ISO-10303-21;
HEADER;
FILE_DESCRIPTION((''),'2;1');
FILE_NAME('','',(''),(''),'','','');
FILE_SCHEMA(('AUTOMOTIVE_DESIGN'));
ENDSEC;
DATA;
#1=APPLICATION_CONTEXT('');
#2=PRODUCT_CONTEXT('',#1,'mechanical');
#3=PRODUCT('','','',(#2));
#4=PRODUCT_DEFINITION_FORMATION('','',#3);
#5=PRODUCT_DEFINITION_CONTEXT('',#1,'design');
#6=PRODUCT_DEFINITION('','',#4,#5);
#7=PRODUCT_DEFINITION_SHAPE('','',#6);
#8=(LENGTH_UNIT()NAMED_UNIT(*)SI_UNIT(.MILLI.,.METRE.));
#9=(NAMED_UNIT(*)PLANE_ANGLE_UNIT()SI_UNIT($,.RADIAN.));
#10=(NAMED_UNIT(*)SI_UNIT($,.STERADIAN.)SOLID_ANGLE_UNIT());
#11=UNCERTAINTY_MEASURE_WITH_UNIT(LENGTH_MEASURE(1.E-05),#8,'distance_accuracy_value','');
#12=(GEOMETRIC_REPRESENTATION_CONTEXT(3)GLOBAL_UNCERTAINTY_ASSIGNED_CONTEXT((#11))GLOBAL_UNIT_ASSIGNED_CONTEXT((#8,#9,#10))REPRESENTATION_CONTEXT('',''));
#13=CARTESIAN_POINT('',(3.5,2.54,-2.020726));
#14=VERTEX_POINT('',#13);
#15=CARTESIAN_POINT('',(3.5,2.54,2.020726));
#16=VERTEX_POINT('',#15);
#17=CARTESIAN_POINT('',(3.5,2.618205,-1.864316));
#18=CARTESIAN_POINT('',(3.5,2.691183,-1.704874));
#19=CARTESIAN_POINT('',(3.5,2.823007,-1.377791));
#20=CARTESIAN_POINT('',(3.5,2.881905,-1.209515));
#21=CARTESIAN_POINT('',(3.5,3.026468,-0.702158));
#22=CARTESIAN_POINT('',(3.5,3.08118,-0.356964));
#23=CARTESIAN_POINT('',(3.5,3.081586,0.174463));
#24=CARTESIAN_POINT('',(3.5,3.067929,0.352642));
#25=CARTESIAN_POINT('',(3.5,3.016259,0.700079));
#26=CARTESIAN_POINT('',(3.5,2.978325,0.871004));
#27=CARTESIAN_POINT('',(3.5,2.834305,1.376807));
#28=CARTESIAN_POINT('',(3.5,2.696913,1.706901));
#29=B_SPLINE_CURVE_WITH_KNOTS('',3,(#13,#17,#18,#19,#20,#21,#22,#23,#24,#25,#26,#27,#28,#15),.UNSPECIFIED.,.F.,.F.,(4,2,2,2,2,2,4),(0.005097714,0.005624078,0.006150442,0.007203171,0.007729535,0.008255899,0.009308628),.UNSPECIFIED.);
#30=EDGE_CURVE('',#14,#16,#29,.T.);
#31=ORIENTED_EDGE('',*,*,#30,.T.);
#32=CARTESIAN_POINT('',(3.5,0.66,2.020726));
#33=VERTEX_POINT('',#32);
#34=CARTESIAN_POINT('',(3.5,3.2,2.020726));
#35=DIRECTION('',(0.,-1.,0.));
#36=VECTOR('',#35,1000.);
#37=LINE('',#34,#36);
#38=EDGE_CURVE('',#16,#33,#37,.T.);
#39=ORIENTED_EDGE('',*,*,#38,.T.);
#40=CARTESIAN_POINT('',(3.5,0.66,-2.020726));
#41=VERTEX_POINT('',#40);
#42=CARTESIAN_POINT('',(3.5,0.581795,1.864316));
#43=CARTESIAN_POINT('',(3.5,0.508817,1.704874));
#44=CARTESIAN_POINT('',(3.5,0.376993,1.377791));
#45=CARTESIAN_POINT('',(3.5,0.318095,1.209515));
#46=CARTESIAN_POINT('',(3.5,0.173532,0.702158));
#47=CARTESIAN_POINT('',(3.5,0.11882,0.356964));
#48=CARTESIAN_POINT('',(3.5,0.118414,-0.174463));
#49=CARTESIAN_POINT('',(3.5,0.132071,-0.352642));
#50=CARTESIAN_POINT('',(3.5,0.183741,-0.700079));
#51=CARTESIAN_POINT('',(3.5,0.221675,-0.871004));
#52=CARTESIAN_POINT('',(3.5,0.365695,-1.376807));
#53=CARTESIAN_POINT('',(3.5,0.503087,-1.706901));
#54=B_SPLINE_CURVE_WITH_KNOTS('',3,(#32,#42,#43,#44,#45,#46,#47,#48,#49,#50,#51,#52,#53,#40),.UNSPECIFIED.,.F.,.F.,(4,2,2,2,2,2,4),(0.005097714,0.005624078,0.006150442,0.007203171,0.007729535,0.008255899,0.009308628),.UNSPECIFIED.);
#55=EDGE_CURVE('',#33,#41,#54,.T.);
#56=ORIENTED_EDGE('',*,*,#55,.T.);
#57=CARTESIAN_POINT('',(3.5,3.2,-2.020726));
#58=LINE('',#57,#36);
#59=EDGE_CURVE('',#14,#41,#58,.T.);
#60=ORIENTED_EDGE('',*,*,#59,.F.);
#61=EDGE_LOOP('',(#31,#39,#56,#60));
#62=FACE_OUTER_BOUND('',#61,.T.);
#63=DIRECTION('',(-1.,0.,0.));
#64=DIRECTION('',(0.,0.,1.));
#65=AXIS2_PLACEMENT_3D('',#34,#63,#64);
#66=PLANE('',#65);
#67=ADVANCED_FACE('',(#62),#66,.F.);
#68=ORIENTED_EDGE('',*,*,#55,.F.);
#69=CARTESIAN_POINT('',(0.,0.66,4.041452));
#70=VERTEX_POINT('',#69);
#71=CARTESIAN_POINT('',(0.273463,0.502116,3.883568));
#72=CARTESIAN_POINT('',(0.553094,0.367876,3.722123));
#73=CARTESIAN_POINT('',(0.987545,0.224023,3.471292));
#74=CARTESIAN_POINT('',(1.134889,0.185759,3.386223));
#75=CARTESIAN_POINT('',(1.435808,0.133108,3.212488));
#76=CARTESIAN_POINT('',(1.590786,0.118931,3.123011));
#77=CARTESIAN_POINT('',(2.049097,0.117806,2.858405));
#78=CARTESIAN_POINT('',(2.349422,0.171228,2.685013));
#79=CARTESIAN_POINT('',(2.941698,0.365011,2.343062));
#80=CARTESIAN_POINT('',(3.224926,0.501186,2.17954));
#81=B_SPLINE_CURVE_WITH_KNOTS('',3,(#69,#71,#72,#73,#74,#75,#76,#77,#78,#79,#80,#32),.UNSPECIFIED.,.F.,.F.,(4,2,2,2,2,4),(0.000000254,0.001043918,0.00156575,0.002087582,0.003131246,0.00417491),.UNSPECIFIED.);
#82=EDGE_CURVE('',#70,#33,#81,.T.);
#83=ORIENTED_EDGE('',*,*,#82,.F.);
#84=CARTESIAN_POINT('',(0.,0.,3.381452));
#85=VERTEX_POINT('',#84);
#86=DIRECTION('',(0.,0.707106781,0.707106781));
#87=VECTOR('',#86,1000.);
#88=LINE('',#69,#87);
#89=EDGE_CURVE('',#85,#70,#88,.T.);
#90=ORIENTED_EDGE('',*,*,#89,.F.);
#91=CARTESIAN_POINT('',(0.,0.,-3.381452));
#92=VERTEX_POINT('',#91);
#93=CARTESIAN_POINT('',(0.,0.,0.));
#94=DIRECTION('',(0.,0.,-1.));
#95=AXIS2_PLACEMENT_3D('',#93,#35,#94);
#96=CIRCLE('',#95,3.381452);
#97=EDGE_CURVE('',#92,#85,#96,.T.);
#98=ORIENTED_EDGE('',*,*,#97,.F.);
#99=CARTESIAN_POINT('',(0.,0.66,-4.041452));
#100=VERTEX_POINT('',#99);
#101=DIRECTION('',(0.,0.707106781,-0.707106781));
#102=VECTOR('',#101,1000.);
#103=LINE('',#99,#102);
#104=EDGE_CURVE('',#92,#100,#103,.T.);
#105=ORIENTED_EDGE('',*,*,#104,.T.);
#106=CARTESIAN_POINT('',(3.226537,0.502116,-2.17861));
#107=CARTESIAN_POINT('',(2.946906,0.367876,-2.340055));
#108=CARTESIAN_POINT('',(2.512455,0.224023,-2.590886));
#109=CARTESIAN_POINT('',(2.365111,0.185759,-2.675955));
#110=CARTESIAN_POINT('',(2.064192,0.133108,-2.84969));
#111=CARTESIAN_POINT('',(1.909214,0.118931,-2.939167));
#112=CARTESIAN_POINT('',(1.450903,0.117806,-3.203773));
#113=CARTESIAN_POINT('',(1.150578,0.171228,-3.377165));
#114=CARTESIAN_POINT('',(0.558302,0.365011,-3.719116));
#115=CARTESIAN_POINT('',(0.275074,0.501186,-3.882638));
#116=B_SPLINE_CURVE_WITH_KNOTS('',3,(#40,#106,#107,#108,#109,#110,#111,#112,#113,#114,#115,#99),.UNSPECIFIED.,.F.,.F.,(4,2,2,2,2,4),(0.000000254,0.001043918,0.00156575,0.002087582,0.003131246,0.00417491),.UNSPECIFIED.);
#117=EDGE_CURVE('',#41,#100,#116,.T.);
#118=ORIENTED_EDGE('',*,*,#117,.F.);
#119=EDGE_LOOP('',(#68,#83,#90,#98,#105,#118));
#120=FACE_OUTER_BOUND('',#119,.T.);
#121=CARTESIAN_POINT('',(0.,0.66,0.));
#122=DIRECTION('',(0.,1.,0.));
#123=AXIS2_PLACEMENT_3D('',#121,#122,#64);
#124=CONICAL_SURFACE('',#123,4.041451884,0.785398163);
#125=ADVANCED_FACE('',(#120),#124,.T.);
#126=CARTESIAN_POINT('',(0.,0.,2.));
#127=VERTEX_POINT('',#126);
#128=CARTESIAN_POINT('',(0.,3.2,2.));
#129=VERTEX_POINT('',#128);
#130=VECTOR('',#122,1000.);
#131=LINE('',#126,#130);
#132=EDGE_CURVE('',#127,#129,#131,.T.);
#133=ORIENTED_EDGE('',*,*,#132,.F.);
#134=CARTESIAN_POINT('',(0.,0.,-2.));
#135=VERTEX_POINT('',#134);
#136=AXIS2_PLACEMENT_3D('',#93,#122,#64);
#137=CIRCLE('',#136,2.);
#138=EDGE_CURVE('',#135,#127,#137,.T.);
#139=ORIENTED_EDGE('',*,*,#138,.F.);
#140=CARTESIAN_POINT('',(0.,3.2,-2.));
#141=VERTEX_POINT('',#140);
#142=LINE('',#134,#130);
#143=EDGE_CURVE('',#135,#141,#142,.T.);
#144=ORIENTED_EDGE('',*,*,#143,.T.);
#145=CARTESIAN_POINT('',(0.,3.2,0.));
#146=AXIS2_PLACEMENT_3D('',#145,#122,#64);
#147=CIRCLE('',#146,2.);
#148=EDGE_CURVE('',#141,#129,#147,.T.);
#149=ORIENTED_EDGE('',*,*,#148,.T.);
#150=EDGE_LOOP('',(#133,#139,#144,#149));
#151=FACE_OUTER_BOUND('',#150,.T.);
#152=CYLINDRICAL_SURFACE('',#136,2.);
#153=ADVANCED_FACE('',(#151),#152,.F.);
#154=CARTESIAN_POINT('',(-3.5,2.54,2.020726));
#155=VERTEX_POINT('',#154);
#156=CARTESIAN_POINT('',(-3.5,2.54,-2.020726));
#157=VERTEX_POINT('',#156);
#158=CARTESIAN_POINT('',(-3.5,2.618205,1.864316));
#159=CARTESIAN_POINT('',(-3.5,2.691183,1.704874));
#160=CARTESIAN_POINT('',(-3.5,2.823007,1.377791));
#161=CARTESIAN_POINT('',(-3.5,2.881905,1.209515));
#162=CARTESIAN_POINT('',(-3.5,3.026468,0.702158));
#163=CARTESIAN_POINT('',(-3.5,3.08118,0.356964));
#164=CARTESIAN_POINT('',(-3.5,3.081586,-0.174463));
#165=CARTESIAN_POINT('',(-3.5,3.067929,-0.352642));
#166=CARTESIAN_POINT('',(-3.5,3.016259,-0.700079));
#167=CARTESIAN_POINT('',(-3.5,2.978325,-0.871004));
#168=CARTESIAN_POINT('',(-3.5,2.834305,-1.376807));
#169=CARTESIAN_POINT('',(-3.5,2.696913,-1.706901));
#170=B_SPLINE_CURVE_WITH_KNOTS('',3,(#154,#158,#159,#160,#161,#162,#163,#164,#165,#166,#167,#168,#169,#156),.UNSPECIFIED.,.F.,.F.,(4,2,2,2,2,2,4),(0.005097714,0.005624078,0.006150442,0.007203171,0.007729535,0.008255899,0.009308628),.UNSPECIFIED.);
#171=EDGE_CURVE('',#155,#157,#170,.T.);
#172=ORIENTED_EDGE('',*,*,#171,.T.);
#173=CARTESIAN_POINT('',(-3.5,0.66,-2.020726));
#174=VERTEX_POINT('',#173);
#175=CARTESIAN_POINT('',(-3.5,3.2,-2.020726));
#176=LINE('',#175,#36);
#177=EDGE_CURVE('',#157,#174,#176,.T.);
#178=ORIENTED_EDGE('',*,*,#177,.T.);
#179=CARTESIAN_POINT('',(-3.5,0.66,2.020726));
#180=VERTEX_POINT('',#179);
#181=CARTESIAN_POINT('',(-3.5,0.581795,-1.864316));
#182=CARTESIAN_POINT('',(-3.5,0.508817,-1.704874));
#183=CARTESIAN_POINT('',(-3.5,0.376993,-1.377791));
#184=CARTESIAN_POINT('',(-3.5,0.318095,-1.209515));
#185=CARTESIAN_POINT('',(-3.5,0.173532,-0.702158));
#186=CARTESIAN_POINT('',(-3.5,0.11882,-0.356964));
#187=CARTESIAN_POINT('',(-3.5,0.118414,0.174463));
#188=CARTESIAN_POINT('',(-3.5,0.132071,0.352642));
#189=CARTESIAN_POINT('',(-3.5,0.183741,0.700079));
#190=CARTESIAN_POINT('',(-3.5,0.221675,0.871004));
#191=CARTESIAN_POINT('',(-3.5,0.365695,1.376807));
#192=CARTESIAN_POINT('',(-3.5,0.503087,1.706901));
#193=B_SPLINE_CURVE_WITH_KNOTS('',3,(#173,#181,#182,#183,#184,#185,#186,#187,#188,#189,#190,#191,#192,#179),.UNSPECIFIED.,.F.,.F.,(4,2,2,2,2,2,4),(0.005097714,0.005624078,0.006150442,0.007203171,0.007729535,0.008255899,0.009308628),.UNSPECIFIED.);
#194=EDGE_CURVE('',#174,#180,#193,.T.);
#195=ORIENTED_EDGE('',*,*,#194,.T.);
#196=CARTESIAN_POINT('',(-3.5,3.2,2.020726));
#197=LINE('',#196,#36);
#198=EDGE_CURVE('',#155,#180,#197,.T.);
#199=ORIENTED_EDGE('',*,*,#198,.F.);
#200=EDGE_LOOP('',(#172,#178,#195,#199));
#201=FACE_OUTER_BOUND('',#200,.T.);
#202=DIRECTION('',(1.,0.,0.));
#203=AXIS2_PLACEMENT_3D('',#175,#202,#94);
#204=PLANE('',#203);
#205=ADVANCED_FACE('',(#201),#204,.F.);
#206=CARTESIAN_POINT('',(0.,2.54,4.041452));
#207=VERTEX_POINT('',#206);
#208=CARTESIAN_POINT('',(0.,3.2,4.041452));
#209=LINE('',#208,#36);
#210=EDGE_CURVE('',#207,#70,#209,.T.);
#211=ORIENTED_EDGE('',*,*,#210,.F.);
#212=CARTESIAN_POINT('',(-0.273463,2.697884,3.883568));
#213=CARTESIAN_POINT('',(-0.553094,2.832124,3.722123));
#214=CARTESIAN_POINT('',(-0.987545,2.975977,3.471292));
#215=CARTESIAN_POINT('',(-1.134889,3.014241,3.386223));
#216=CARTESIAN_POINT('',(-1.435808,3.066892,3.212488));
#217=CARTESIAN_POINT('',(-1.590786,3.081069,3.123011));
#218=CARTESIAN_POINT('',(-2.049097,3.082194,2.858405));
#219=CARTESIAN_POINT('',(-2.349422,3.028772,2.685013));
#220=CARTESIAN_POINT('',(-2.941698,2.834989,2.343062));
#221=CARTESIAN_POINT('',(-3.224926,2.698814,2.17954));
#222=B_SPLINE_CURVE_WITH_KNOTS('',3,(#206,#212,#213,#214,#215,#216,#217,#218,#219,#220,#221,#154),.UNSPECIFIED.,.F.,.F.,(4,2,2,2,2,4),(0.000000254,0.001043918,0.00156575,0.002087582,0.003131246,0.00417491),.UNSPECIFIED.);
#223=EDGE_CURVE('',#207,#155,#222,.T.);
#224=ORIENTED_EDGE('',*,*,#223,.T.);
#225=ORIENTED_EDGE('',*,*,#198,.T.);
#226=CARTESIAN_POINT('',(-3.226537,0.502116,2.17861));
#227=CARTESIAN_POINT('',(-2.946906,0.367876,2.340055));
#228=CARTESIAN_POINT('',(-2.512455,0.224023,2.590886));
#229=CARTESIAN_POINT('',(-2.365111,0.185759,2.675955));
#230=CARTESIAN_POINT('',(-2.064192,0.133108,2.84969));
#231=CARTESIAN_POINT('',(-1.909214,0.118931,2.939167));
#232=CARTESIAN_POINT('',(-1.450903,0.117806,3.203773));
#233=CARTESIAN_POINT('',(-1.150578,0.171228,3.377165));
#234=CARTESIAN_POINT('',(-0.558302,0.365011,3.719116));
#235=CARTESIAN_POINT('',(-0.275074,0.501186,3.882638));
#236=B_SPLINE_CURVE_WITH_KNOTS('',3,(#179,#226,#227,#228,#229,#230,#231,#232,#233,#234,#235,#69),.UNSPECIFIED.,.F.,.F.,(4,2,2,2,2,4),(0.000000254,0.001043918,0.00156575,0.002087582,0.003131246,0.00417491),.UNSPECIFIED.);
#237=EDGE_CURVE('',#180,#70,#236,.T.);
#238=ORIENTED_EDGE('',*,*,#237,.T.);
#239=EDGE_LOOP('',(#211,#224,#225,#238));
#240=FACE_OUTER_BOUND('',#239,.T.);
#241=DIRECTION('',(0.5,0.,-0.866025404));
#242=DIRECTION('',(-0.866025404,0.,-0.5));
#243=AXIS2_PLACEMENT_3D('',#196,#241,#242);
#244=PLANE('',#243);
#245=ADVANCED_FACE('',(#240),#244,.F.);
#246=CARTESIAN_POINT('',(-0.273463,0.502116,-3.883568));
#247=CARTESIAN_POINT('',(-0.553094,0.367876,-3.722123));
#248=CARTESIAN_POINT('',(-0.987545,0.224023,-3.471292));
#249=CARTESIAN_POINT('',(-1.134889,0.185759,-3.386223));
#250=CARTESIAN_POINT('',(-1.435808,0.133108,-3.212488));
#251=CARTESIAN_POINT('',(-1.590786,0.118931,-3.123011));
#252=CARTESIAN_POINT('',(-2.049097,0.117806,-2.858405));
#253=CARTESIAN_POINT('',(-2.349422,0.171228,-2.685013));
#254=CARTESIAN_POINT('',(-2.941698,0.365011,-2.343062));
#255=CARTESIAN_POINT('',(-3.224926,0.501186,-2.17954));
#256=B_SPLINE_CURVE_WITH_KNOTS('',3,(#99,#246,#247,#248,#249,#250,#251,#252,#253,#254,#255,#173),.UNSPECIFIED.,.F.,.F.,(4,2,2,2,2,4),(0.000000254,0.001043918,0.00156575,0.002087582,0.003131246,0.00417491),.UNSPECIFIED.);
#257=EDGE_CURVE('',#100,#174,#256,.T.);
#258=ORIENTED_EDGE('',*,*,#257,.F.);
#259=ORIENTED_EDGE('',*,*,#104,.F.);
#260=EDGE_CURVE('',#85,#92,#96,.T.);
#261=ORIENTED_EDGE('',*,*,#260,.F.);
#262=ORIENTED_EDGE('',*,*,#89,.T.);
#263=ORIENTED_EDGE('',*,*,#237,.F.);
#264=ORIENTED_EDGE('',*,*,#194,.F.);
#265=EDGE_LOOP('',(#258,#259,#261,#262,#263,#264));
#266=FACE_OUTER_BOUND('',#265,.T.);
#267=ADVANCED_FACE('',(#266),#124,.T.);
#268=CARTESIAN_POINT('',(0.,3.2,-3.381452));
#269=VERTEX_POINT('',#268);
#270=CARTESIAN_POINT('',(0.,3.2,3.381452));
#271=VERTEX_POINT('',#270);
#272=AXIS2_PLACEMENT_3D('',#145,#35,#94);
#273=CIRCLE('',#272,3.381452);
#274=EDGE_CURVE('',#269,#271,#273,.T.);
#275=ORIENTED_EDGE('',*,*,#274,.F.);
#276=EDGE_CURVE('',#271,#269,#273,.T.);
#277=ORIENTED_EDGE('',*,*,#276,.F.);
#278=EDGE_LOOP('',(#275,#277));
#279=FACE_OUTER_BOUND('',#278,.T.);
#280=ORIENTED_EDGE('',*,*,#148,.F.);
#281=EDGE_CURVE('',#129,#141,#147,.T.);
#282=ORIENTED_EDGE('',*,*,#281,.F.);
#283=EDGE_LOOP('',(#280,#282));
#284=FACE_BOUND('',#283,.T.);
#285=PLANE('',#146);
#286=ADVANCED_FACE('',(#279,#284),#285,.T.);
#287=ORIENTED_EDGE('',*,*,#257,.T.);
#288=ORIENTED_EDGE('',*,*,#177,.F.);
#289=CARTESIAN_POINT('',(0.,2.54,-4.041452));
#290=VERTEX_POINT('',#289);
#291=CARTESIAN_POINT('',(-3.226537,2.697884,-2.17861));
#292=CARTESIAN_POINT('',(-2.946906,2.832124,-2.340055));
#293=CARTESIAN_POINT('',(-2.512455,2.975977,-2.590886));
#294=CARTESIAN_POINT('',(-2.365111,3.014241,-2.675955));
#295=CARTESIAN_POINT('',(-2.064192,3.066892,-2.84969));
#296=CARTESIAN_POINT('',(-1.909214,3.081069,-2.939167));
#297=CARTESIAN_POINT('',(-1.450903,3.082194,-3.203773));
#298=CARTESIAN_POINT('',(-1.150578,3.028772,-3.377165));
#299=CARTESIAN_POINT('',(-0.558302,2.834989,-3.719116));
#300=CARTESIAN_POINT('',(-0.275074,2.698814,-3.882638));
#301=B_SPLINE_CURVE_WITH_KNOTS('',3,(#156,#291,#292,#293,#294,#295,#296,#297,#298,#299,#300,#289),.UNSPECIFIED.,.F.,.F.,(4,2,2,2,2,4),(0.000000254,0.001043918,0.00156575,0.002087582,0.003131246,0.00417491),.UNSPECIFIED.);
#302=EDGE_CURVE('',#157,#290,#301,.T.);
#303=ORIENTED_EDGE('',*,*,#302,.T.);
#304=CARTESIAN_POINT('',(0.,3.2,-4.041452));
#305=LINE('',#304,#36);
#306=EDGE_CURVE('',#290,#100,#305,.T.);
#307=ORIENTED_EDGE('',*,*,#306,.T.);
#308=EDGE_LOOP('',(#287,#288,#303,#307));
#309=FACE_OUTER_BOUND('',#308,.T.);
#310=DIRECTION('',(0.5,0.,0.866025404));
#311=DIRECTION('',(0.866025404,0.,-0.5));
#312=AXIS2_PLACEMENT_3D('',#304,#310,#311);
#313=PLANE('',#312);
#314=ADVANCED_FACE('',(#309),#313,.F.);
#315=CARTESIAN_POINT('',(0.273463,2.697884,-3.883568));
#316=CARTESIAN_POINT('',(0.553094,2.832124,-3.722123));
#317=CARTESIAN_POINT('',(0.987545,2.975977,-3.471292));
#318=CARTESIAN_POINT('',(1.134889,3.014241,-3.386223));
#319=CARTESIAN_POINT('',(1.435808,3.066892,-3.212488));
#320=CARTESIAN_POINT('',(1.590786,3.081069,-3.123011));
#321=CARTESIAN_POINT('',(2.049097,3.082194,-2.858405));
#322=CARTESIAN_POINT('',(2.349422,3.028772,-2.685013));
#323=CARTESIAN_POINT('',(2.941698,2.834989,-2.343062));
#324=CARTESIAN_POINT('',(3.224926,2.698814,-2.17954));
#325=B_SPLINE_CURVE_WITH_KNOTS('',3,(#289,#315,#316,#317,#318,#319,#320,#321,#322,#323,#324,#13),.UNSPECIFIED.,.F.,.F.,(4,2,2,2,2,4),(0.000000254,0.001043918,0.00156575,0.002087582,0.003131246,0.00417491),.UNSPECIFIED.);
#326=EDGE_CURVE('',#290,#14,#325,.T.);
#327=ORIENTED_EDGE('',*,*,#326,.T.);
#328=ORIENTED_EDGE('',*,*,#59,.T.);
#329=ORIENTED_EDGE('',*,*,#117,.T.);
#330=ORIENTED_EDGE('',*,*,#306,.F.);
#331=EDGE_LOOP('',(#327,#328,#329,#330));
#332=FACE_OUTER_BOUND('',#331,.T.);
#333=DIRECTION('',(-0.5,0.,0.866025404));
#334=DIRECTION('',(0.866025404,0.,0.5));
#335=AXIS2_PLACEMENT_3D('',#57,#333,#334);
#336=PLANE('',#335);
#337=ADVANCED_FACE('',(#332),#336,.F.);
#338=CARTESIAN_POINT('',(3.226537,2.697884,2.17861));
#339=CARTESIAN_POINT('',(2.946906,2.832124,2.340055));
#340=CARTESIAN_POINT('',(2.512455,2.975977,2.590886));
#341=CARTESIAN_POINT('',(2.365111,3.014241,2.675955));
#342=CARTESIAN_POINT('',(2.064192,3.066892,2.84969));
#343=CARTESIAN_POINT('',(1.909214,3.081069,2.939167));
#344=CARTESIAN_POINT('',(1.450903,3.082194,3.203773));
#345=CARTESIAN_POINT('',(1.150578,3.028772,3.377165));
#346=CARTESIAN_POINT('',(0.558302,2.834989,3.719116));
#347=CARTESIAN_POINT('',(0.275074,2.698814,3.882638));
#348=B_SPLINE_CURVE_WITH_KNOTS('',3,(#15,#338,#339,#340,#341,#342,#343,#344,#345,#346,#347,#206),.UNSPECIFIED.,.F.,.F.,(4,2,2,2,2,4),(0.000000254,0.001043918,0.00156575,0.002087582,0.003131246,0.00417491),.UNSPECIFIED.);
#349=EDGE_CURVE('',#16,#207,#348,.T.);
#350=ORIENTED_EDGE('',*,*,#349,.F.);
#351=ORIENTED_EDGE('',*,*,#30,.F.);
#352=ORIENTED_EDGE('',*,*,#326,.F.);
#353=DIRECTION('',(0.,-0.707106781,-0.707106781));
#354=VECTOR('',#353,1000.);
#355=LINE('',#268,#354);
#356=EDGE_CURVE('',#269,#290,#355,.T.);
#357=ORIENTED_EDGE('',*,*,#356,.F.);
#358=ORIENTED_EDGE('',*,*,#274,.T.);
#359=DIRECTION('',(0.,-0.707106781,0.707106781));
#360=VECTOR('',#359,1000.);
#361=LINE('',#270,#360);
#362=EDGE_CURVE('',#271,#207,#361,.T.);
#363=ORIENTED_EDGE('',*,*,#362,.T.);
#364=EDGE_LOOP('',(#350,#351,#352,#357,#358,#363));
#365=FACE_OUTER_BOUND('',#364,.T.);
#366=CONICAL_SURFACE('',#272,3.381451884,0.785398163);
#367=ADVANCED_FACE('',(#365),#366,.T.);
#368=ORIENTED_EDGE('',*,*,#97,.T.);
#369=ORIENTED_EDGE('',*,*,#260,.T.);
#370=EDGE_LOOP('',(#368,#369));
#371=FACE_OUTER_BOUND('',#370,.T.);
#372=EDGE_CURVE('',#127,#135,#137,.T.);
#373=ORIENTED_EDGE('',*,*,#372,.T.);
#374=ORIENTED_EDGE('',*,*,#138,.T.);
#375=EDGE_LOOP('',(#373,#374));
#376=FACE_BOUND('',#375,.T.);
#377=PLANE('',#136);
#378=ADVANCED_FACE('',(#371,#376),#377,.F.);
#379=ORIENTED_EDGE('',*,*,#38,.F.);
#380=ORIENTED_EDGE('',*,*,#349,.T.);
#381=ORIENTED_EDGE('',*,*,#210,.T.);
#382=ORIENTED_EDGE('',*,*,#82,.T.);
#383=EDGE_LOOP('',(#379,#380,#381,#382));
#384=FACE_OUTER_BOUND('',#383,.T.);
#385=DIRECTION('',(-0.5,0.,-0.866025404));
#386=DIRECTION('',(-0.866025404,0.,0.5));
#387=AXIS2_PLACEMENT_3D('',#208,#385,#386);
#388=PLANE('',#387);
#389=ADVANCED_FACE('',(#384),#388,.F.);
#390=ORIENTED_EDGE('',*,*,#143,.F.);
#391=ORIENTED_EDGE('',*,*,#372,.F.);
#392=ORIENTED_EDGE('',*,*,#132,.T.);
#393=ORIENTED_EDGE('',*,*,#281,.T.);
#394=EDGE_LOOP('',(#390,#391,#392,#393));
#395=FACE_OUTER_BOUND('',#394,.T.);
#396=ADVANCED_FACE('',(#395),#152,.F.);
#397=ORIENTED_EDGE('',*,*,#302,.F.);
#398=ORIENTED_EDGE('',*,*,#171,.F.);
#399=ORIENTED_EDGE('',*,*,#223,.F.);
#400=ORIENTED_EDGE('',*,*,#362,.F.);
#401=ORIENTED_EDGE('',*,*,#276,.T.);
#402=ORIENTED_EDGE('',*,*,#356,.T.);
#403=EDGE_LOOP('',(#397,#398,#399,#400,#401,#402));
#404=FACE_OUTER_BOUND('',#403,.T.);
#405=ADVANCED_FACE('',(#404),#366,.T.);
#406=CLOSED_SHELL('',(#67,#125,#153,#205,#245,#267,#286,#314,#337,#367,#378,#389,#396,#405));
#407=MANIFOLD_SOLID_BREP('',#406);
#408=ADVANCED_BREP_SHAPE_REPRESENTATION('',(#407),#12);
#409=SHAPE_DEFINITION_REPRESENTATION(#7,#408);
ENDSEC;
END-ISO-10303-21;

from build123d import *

# Parameters (mm, degrees)
BOSS_EXTRUDE1_DEPTH = 3.2
SKETCH8_R           = 2
CUT_EXTRUDE1_DEPTH  = 7.23083729


with BuildPart() as part:
    # Sketch1 → Boss-Extrude1 (new body)
    with BuildSketch(Plane(origin=(0, 0, 0), x_dir=(1, 0, 0), z_dir=(0, 1, 0))):
        Polygon((0, 4.041451884), (-3.5, 2.020725942), (-3.5, -2.020725942), (0, -4.041451884), (3.5, -2.020725942), (3.5, 2.020725942), align=None)
    extrude(amount=BOSS_EXTRUDE1_DEPTH)

    # Sketch3 → Cut-Revolve2 (revolve, cut)
    with BuildSketch(Plane(origin=(0, 0, 0), x_dir=(0.8660254037844417, 0, 0.4999999999999949), z_dir=(-0.4999999999999949, 0, 0.8660254037844417)), mode=Mode.PRIVATE) as cut_revolve2_sk:
        Polygon((4.041451884, 3.2), (4.041451884, 2.54), (3.381451884, 3.2), align=None)
        Polygon((4.041451884, 0), (4.041451884, 0.66), (3.381451884, 0), align=None)
    revolve(cut_revolve2_sk.sketch.rotate(Axis((0, -1.01584762, 0), (0, 1, 0)), 300), axis=Axis((0, -1.01584762, 0), (0, 1, 0)), mode=Mode.SUBTRACT)

    # Sketch8 → Cut-Extrude1 (cut, through all)
    with BuildSketch(Plane(origin=(0, 3.2, 0), x_dir=(1, 0, 0), z_dir=(0, 1, 0))):
        with Locations(Location((0, 0, 0), (0, 0, 270))):
            Circle(SKETCH8_R)
    extrude(amount=-CUT_EXTRUDE1_DEPTH, mode=Mode.SUBTRACT)


solid = part.part
